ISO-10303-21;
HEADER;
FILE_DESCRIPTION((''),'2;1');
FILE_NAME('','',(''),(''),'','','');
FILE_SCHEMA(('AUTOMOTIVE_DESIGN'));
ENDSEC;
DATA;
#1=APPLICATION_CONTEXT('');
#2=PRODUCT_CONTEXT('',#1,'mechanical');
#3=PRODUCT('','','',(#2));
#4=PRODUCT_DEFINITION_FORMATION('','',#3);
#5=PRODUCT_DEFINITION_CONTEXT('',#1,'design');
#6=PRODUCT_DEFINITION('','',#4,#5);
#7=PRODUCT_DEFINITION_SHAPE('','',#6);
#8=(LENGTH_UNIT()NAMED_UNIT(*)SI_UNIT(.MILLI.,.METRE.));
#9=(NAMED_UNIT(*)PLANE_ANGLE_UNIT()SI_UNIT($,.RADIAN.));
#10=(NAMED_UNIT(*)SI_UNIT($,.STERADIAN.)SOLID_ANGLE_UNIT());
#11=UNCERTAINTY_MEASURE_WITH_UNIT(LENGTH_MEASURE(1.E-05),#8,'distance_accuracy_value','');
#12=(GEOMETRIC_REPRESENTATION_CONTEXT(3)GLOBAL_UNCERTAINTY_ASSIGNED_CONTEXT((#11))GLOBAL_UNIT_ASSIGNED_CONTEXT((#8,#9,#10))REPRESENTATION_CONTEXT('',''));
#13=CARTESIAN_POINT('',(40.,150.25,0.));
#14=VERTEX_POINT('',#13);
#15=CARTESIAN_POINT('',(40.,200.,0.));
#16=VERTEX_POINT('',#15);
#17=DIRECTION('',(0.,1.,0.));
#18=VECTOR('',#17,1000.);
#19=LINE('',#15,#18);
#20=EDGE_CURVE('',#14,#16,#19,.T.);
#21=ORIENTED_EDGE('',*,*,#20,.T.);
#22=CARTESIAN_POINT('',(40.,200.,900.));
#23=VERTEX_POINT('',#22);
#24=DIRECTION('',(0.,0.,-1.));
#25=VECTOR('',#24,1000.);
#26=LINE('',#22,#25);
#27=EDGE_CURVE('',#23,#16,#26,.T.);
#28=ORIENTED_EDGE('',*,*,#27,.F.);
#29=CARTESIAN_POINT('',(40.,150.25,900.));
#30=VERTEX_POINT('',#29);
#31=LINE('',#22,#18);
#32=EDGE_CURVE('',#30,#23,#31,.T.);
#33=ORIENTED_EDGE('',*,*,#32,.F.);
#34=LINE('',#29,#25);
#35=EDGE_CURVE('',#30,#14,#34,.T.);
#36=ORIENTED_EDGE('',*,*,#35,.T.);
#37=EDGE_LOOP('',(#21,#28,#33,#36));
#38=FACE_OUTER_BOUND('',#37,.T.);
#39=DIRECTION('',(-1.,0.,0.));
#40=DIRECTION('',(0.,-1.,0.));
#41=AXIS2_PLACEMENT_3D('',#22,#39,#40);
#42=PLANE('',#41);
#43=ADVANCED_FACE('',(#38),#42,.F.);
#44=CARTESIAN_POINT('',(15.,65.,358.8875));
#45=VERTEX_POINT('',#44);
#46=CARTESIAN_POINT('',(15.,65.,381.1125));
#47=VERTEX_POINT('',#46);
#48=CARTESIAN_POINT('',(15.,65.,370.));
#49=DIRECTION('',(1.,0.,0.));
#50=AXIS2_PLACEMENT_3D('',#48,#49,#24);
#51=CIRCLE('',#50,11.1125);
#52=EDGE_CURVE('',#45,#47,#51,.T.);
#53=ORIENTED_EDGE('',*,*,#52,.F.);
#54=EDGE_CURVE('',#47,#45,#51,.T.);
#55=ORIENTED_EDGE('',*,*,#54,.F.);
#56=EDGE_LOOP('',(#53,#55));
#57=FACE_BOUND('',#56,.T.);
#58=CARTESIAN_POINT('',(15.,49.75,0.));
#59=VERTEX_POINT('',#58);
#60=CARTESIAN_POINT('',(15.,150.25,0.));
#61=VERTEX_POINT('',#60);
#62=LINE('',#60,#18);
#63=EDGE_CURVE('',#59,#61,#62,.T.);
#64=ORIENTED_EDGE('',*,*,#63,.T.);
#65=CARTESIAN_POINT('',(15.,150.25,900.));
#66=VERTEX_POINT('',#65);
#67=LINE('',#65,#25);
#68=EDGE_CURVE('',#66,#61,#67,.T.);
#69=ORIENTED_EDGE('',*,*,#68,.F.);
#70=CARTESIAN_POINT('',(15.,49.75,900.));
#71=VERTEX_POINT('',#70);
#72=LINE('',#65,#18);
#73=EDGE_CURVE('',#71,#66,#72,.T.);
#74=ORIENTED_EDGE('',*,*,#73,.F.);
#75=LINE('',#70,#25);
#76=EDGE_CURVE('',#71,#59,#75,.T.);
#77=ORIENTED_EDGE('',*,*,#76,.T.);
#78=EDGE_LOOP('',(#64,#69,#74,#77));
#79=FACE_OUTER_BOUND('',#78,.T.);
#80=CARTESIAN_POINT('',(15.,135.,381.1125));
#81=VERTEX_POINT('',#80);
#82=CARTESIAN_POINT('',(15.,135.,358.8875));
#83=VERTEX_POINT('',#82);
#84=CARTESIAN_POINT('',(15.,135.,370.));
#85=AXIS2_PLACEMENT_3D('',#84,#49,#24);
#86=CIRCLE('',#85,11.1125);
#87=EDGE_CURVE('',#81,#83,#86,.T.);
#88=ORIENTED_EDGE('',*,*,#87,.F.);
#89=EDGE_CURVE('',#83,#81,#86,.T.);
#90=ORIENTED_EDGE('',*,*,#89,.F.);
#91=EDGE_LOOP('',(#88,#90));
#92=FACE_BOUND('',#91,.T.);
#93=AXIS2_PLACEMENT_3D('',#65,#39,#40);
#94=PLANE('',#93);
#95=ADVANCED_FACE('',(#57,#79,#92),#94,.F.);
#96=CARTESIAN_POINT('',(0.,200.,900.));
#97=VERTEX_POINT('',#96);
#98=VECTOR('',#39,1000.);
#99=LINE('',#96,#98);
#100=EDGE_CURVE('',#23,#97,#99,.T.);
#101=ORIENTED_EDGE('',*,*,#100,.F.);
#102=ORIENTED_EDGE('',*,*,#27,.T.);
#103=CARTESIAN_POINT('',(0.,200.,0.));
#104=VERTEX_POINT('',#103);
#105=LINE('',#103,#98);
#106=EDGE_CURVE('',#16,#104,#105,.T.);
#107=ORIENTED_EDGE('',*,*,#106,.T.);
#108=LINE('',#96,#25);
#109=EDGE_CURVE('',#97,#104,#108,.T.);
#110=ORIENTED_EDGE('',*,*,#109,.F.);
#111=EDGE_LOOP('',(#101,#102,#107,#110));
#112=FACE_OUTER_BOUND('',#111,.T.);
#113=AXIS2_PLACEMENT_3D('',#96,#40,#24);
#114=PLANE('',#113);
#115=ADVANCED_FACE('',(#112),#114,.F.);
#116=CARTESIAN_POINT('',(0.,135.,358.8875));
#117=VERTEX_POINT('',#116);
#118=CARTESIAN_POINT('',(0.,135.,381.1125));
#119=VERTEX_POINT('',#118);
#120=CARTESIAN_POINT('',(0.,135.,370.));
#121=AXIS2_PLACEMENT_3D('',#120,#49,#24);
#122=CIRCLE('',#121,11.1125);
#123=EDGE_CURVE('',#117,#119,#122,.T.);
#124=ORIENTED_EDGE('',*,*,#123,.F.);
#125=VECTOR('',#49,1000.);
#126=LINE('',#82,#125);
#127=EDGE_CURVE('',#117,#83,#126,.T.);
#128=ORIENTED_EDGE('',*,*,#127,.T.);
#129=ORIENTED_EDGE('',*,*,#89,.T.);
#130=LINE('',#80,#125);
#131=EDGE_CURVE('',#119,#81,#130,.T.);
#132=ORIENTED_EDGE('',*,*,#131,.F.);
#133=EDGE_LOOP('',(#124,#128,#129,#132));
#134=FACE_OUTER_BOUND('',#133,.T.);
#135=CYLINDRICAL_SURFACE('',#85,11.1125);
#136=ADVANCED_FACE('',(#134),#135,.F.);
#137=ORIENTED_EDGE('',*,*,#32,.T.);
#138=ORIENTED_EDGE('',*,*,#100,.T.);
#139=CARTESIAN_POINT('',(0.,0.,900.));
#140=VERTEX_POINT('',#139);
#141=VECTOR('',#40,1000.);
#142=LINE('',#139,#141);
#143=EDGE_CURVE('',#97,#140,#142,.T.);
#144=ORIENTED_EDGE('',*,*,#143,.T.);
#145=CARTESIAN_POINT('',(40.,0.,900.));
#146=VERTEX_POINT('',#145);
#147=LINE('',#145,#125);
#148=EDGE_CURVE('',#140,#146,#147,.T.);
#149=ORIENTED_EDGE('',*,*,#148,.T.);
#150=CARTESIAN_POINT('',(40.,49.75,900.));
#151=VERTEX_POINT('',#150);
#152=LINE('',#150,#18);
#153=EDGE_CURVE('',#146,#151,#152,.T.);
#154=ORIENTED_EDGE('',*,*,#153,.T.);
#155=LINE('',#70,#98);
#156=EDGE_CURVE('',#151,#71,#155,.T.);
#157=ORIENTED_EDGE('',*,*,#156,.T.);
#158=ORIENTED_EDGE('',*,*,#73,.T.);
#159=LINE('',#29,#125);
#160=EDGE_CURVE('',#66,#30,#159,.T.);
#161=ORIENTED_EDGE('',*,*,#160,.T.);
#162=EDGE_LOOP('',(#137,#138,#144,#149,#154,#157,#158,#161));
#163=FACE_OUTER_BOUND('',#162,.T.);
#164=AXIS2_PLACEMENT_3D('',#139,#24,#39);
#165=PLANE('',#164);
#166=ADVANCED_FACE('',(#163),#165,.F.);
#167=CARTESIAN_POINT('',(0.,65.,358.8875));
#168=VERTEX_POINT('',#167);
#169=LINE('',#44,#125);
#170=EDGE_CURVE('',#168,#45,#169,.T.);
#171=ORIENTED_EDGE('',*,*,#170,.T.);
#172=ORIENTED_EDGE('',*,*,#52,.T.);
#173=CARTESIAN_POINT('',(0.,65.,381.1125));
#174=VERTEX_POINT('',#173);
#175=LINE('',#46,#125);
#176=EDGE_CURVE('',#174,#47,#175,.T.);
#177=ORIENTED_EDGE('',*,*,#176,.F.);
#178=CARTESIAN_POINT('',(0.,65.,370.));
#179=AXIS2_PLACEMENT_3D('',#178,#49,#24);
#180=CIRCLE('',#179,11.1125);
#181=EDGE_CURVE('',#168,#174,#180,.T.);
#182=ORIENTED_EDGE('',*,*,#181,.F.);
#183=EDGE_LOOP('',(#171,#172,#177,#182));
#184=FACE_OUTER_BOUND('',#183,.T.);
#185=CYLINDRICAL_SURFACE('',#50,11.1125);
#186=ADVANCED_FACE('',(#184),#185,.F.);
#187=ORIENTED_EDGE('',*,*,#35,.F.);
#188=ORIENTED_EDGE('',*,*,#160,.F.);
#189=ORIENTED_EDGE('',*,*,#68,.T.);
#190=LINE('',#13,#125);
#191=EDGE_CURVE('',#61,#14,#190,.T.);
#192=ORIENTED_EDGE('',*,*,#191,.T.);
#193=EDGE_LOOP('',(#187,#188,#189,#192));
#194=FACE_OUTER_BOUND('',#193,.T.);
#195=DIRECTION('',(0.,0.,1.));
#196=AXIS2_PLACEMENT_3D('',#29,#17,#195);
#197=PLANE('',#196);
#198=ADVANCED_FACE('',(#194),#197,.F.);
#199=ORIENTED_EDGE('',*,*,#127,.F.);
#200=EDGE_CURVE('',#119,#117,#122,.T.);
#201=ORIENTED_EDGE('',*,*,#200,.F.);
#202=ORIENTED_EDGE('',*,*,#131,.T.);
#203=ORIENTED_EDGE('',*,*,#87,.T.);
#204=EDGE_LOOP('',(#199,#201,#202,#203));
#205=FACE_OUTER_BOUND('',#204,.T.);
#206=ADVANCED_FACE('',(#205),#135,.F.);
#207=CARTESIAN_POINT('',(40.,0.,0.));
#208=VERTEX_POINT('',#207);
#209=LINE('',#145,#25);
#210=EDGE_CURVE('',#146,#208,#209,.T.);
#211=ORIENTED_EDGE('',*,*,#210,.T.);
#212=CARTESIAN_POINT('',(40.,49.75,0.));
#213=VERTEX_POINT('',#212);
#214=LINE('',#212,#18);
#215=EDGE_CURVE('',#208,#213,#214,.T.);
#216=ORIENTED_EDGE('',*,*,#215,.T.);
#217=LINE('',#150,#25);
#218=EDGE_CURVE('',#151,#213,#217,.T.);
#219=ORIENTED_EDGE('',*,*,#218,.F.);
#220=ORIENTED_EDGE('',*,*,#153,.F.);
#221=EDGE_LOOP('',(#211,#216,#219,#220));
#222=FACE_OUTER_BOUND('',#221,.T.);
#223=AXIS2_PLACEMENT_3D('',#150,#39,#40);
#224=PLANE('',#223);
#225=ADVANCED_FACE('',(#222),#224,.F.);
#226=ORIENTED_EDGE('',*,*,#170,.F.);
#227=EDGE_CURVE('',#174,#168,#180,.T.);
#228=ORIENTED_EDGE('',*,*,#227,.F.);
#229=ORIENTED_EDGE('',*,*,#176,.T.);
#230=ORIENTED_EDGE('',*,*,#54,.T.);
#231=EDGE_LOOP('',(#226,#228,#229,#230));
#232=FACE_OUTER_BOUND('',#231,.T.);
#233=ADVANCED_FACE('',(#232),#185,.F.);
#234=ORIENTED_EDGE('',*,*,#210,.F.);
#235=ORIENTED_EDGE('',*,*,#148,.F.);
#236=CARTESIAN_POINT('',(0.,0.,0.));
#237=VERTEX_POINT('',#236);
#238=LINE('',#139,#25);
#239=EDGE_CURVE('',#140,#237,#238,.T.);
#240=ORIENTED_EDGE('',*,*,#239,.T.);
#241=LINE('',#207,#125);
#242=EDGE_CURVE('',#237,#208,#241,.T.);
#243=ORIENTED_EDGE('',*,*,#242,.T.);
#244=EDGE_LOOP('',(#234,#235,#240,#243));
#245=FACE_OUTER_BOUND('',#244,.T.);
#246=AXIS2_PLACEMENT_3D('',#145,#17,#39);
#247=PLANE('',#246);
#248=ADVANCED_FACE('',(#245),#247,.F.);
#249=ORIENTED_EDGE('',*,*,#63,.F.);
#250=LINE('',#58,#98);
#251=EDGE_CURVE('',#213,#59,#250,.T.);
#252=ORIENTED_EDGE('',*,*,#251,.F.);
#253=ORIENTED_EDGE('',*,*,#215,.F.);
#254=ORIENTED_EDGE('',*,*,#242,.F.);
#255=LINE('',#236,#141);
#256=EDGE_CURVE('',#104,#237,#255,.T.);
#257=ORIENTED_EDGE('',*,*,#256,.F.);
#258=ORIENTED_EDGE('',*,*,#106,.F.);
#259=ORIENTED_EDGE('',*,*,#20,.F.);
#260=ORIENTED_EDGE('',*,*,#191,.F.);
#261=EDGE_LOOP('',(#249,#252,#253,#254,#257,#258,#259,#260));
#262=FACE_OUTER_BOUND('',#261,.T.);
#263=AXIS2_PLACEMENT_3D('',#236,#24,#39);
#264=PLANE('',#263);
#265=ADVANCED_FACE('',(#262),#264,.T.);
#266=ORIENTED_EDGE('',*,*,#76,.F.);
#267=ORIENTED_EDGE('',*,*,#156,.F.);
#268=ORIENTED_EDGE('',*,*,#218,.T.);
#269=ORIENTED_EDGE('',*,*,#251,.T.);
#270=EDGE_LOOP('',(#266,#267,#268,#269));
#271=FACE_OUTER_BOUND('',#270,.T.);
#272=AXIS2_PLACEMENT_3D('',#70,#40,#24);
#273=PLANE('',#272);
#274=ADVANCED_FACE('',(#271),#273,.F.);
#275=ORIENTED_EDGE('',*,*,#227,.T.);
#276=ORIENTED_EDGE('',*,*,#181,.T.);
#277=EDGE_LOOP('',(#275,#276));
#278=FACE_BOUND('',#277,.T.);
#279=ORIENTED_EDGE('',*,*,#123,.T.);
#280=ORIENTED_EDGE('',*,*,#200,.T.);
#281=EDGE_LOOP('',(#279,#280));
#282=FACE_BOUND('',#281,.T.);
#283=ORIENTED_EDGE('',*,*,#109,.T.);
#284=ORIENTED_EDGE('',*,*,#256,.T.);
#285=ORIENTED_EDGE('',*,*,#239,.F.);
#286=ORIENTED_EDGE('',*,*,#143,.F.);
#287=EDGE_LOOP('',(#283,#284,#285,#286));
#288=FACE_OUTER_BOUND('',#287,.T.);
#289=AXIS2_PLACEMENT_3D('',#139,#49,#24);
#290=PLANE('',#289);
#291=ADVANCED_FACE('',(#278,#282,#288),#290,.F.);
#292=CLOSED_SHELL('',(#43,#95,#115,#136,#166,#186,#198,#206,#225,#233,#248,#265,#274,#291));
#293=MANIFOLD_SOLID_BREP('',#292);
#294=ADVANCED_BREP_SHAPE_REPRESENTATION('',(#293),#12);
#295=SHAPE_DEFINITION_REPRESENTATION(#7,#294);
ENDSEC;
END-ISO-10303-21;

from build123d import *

# Parameters (mm, degrees)
BOSS_EXTRUDE1_DEPTH  = 900
F_1_8_TAPPED_HOLE1_D = 22.225


with BuildPart() as part:
    # Sketch1 → Boss-Extrude1 (new body)
    with BuildSketch(Plane.XY):
        Polygon((0, 0), (0, 200), (40, 200), (40, 150.25), (15, 150.25), (15, 49.75), (40, 49.75), (40, 0), align=None)
    extrude(amount=BOSS_EXTRUDE1_DEPTH)

    # 1-8 Tapped Hole1 (through all)
    with Locations(Plane(origin=(15, 135, 370), x_dir=(0, 1, 0), z_dir=(1, 0, 0))):
        with Locations((0, 0), (-70, 0)):
            Hole(F_1_8_TAPPED_HOLE1_D / 2)


solid = part.part
